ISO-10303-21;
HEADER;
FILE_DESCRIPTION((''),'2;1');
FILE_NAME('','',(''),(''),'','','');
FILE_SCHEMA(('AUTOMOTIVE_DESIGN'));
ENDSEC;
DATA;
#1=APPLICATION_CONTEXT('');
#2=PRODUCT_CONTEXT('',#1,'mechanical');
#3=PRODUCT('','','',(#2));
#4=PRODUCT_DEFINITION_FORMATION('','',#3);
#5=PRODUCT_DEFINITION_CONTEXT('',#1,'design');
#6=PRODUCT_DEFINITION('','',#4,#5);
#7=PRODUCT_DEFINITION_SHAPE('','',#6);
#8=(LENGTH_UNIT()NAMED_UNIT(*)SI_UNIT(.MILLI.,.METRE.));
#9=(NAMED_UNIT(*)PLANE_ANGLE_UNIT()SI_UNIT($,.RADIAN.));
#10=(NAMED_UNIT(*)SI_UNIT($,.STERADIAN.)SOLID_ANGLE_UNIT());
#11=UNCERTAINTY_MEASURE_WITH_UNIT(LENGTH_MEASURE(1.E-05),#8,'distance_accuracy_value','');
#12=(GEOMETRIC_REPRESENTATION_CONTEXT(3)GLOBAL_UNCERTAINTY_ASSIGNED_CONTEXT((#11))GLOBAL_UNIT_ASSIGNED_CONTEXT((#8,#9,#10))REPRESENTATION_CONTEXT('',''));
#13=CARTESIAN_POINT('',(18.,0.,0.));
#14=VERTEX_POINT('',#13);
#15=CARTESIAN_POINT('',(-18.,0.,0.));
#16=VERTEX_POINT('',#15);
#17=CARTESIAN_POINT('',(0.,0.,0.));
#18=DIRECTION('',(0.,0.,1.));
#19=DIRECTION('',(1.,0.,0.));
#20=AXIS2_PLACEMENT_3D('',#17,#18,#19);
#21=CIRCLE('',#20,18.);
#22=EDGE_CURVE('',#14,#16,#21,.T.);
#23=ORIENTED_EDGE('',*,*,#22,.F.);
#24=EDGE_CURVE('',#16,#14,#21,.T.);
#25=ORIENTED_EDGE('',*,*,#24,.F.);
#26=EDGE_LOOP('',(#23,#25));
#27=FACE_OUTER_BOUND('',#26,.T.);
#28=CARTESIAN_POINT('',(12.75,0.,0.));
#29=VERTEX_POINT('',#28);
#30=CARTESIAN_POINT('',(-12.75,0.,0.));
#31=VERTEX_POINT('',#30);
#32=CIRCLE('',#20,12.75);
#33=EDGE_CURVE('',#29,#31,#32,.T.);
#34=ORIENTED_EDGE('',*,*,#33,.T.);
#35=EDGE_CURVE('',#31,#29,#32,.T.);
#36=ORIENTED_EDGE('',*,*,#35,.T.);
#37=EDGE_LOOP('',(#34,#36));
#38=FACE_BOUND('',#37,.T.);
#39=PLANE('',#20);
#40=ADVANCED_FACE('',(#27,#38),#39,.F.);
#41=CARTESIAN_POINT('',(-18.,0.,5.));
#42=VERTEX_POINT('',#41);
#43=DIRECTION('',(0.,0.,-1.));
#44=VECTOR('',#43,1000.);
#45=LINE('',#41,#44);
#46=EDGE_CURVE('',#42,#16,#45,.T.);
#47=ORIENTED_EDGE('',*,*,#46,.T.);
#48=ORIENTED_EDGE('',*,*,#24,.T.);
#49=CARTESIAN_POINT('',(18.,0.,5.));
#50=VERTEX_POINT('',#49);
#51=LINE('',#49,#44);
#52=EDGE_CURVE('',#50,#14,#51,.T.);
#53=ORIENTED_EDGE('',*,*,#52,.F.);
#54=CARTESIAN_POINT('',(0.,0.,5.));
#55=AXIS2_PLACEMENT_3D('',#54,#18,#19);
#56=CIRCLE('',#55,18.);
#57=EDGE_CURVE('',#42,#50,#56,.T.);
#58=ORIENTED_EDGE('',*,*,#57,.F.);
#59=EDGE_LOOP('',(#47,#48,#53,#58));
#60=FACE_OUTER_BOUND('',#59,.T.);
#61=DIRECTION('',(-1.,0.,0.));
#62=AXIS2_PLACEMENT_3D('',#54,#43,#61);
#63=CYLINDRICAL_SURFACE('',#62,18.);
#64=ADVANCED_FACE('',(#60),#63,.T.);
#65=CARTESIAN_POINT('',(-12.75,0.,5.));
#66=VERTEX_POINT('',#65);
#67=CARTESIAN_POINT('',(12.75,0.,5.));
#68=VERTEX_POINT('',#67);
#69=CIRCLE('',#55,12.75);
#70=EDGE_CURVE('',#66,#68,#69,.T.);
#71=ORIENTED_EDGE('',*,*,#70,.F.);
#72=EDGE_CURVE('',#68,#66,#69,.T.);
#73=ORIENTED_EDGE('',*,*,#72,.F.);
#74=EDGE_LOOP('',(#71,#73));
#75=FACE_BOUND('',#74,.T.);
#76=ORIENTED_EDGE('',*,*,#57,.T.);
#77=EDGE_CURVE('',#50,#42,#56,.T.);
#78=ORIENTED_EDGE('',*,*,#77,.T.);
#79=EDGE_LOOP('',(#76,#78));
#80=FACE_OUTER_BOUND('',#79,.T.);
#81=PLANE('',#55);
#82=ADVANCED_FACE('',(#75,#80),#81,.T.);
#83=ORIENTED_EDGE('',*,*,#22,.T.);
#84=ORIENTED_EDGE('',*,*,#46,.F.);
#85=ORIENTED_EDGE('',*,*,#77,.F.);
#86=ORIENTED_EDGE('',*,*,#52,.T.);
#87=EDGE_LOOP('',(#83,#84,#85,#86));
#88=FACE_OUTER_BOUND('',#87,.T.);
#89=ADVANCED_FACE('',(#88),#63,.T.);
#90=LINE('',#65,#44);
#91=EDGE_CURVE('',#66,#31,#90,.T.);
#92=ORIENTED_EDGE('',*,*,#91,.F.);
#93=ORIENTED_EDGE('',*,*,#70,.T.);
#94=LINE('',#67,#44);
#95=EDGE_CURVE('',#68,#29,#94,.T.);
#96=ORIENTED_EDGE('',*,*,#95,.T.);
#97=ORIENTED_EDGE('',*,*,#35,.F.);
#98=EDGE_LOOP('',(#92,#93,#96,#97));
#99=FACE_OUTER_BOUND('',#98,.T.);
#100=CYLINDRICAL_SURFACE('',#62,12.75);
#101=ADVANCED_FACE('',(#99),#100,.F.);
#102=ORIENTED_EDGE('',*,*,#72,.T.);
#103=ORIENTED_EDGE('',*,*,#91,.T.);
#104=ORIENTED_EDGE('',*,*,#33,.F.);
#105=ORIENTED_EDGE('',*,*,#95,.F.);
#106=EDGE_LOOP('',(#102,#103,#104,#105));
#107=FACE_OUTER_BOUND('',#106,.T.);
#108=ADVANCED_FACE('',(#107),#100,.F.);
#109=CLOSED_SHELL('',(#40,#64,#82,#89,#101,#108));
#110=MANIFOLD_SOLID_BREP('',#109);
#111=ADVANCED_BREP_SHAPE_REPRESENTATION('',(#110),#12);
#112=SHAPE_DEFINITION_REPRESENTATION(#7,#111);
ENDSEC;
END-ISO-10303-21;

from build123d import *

# Parameters (mm, degrees)
SKETCH1_R           = 18
SKETCH1_R_2         = 12.75
BOSS_EXTRUDE1_DEPTH = 5


with BuildPart() as part:
    # Sketch1 → Boss-Extrude1 (new body)
    with BuildSketch(Plane.XY):
        Circle(SKETCH1_R)
        Circle(SKETCH1_R_2, mode=Mode.SUBTRACT)
    extrude(amount=BOSS_EXTRUDE1_DEPTH)


solid = part.part
